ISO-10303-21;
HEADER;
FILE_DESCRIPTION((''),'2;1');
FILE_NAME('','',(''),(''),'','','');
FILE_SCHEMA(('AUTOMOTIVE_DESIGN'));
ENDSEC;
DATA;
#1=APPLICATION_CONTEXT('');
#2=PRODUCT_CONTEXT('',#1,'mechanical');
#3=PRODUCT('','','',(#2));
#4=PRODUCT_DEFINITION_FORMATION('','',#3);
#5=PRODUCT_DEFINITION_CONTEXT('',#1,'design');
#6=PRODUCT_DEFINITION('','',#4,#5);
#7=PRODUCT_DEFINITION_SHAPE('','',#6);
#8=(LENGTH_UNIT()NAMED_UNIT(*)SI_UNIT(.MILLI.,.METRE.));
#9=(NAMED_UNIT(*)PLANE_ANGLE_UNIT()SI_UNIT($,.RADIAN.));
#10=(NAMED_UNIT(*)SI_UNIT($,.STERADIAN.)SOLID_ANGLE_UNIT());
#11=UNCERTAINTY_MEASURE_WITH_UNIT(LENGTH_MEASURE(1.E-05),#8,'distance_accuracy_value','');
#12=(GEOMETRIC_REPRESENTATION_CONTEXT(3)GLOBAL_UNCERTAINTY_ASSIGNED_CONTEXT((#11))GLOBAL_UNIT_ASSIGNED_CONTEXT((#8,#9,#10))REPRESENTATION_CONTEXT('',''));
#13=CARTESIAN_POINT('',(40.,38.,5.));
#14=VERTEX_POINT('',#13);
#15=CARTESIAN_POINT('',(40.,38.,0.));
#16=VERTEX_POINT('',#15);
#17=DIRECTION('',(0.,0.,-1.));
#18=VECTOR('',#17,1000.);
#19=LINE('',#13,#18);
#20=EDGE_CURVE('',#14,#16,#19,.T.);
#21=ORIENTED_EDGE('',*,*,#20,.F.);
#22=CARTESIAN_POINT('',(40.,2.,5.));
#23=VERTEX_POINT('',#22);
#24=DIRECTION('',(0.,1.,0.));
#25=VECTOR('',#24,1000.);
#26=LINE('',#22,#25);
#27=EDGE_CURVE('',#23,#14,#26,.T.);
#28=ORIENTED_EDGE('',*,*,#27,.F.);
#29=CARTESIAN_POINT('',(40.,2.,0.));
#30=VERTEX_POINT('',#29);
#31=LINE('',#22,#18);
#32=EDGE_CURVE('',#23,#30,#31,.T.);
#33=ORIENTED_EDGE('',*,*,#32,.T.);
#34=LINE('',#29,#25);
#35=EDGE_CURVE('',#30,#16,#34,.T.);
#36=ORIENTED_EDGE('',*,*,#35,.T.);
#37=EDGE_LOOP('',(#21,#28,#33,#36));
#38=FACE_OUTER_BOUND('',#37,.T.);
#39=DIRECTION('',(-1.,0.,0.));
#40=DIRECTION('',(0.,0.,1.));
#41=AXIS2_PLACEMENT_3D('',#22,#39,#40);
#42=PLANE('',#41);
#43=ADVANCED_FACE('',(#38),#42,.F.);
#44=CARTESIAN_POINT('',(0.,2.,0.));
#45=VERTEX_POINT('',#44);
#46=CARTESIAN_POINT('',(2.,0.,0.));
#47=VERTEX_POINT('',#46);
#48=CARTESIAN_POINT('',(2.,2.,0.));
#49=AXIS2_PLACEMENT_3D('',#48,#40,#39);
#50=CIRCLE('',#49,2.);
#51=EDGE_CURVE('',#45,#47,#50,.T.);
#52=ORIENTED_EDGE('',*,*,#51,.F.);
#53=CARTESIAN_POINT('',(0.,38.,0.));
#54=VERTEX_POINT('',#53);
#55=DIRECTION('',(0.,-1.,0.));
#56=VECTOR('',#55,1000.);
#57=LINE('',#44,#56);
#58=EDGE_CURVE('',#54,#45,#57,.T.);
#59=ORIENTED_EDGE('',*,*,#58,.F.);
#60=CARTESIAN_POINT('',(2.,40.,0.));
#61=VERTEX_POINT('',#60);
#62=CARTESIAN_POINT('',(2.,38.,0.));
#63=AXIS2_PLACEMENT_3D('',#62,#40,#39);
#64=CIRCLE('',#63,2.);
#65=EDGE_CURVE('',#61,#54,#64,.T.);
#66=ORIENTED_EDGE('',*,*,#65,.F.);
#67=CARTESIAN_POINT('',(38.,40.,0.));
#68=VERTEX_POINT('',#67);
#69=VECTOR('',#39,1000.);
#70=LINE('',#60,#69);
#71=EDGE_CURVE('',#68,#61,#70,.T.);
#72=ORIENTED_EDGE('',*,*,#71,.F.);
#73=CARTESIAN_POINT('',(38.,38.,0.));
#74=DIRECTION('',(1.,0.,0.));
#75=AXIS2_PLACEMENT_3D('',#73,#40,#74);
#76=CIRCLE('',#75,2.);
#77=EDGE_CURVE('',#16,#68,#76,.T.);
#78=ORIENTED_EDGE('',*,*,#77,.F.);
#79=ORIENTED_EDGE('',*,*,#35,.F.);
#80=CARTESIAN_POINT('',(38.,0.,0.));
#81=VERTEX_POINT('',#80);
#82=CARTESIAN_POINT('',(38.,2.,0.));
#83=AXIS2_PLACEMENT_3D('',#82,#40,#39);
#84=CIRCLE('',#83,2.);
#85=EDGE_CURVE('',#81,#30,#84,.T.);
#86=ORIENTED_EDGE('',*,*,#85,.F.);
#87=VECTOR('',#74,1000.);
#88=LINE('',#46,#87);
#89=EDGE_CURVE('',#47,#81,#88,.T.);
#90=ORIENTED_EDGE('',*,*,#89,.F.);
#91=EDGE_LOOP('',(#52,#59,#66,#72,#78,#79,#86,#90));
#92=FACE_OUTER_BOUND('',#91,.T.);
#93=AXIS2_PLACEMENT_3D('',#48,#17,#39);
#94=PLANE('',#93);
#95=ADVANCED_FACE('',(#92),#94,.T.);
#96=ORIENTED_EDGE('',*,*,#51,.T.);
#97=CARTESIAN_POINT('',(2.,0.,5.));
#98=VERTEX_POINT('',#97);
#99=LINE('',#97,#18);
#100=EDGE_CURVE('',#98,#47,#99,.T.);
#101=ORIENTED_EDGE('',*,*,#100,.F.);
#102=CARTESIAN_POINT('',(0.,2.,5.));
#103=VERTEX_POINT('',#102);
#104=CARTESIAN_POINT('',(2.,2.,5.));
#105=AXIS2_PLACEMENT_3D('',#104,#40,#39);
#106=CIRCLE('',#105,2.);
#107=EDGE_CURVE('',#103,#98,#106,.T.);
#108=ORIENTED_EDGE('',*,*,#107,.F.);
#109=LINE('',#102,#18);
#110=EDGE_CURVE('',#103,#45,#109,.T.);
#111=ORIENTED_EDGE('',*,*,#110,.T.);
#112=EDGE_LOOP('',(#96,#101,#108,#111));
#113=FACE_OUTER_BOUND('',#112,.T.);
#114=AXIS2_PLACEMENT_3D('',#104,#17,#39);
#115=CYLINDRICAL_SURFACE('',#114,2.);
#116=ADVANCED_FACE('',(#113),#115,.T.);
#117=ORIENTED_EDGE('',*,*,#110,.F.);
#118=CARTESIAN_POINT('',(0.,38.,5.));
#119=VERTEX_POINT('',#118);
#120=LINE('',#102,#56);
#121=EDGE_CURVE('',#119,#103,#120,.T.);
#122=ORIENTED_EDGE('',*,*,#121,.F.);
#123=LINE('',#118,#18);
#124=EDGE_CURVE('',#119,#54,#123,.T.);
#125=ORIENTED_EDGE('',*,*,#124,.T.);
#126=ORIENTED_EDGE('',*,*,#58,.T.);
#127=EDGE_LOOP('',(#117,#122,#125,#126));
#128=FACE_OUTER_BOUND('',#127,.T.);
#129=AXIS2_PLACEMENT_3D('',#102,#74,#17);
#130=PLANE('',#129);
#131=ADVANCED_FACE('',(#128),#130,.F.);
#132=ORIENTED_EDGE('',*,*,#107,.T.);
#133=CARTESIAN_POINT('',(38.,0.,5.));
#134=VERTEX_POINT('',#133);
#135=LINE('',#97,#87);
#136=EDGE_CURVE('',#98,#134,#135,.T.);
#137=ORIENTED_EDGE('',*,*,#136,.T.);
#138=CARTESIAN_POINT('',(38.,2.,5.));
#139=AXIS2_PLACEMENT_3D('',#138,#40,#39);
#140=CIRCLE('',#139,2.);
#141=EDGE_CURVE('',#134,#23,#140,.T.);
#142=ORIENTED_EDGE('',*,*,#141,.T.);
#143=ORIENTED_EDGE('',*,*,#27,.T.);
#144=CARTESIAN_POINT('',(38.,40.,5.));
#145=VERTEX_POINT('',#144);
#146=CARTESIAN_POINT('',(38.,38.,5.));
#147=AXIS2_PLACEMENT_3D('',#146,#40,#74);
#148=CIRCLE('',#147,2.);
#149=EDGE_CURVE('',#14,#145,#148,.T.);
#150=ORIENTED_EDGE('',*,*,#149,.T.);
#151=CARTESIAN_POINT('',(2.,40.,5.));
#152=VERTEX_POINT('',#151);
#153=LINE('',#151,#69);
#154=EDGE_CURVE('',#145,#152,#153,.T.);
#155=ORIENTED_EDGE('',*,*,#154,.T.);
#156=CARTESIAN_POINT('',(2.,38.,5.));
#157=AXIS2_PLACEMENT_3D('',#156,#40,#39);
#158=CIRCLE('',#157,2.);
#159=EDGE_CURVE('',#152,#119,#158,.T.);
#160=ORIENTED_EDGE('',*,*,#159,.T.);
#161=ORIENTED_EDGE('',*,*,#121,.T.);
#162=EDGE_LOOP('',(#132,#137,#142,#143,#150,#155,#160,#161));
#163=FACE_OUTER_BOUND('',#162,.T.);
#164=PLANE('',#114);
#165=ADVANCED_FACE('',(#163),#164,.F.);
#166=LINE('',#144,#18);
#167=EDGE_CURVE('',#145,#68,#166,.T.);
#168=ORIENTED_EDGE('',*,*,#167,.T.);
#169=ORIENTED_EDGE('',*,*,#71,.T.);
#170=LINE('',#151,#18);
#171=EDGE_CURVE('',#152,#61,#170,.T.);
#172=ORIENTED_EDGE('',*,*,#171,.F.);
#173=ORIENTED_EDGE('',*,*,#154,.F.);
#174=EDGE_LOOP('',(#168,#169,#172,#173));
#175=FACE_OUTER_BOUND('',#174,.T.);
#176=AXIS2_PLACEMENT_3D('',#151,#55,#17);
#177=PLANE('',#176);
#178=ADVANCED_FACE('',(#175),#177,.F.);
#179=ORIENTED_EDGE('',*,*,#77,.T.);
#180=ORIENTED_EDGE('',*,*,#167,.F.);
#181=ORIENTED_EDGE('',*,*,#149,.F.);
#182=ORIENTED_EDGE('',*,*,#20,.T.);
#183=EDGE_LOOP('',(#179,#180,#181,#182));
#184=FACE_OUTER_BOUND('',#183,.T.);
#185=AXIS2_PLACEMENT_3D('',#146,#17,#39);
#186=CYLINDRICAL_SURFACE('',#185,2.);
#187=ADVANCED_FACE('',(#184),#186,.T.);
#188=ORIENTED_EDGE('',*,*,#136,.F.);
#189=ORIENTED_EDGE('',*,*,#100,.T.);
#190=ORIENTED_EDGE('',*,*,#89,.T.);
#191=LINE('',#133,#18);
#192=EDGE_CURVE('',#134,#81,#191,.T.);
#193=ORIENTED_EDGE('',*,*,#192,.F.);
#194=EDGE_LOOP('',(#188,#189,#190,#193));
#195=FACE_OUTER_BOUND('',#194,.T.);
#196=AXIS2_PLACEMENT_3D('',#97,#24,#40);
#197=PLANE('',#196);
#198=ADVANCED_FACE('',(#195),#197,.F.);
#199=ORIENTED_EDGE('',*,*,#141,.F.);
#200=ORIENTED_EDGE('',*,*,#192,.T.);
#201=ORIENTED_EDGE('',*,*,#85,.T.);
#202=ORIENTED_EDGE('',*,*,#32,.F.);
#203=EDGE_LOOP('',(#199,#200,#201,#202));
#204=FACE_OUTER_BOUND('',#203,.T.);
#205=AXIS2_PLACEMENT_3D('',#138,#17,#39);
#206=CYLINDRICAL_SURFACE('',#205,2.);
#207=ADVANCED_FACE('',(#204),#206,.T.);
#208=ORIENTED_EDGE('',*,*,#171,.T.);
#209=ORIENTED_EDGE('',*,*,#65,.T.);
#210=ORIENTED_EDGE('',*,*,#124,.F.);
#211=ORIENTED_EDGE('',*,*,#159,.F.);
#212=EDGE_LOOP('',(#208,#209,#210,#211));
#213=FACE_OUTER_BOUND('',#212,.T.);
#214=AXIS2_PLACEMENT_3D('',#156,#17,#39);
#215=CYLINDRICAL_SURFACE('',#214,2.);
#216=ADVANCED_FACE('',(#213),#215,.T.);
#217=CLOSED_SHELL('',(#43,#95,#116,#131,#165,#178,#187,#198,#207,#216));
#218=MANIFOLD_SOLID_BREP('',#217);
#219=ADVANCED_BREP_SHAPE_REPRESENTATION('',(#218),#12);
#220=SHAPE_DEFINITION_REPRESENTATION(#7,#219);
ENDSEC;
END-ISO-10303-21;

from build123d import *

# Parameters (mm, degrees)
BOSS_EXTRUDE1_DEPTH = 5


with BuildPart() as part:
    # Sketch1 → Boss-Extrude1 (new body)
    with BuildSketch(Plane.XY):
        with BuildLine():
            Line((2, 0), (38, 0))
            ThreePointArc((38, 0), (39.414213562, 0.585786438), (40, 2))
            Line((40, 2), (40, 38))
            ThreePointArc((40, 38), (39.414213562, 39.414213562), (38, 40))
            Line((38, 40), (2, 40))
            ThreePointArc((2, 40), (0.585786438, 39.414213562), (0, 38))
            Line((0, 38), (0, 2))
            ThreePointArc((0, 2), (0.585786438, 0.585786438), (2, 0))
        make_face()
    extrude(amount=BOSS_EXTRUDE1_DEPTH)


solid = part.part
